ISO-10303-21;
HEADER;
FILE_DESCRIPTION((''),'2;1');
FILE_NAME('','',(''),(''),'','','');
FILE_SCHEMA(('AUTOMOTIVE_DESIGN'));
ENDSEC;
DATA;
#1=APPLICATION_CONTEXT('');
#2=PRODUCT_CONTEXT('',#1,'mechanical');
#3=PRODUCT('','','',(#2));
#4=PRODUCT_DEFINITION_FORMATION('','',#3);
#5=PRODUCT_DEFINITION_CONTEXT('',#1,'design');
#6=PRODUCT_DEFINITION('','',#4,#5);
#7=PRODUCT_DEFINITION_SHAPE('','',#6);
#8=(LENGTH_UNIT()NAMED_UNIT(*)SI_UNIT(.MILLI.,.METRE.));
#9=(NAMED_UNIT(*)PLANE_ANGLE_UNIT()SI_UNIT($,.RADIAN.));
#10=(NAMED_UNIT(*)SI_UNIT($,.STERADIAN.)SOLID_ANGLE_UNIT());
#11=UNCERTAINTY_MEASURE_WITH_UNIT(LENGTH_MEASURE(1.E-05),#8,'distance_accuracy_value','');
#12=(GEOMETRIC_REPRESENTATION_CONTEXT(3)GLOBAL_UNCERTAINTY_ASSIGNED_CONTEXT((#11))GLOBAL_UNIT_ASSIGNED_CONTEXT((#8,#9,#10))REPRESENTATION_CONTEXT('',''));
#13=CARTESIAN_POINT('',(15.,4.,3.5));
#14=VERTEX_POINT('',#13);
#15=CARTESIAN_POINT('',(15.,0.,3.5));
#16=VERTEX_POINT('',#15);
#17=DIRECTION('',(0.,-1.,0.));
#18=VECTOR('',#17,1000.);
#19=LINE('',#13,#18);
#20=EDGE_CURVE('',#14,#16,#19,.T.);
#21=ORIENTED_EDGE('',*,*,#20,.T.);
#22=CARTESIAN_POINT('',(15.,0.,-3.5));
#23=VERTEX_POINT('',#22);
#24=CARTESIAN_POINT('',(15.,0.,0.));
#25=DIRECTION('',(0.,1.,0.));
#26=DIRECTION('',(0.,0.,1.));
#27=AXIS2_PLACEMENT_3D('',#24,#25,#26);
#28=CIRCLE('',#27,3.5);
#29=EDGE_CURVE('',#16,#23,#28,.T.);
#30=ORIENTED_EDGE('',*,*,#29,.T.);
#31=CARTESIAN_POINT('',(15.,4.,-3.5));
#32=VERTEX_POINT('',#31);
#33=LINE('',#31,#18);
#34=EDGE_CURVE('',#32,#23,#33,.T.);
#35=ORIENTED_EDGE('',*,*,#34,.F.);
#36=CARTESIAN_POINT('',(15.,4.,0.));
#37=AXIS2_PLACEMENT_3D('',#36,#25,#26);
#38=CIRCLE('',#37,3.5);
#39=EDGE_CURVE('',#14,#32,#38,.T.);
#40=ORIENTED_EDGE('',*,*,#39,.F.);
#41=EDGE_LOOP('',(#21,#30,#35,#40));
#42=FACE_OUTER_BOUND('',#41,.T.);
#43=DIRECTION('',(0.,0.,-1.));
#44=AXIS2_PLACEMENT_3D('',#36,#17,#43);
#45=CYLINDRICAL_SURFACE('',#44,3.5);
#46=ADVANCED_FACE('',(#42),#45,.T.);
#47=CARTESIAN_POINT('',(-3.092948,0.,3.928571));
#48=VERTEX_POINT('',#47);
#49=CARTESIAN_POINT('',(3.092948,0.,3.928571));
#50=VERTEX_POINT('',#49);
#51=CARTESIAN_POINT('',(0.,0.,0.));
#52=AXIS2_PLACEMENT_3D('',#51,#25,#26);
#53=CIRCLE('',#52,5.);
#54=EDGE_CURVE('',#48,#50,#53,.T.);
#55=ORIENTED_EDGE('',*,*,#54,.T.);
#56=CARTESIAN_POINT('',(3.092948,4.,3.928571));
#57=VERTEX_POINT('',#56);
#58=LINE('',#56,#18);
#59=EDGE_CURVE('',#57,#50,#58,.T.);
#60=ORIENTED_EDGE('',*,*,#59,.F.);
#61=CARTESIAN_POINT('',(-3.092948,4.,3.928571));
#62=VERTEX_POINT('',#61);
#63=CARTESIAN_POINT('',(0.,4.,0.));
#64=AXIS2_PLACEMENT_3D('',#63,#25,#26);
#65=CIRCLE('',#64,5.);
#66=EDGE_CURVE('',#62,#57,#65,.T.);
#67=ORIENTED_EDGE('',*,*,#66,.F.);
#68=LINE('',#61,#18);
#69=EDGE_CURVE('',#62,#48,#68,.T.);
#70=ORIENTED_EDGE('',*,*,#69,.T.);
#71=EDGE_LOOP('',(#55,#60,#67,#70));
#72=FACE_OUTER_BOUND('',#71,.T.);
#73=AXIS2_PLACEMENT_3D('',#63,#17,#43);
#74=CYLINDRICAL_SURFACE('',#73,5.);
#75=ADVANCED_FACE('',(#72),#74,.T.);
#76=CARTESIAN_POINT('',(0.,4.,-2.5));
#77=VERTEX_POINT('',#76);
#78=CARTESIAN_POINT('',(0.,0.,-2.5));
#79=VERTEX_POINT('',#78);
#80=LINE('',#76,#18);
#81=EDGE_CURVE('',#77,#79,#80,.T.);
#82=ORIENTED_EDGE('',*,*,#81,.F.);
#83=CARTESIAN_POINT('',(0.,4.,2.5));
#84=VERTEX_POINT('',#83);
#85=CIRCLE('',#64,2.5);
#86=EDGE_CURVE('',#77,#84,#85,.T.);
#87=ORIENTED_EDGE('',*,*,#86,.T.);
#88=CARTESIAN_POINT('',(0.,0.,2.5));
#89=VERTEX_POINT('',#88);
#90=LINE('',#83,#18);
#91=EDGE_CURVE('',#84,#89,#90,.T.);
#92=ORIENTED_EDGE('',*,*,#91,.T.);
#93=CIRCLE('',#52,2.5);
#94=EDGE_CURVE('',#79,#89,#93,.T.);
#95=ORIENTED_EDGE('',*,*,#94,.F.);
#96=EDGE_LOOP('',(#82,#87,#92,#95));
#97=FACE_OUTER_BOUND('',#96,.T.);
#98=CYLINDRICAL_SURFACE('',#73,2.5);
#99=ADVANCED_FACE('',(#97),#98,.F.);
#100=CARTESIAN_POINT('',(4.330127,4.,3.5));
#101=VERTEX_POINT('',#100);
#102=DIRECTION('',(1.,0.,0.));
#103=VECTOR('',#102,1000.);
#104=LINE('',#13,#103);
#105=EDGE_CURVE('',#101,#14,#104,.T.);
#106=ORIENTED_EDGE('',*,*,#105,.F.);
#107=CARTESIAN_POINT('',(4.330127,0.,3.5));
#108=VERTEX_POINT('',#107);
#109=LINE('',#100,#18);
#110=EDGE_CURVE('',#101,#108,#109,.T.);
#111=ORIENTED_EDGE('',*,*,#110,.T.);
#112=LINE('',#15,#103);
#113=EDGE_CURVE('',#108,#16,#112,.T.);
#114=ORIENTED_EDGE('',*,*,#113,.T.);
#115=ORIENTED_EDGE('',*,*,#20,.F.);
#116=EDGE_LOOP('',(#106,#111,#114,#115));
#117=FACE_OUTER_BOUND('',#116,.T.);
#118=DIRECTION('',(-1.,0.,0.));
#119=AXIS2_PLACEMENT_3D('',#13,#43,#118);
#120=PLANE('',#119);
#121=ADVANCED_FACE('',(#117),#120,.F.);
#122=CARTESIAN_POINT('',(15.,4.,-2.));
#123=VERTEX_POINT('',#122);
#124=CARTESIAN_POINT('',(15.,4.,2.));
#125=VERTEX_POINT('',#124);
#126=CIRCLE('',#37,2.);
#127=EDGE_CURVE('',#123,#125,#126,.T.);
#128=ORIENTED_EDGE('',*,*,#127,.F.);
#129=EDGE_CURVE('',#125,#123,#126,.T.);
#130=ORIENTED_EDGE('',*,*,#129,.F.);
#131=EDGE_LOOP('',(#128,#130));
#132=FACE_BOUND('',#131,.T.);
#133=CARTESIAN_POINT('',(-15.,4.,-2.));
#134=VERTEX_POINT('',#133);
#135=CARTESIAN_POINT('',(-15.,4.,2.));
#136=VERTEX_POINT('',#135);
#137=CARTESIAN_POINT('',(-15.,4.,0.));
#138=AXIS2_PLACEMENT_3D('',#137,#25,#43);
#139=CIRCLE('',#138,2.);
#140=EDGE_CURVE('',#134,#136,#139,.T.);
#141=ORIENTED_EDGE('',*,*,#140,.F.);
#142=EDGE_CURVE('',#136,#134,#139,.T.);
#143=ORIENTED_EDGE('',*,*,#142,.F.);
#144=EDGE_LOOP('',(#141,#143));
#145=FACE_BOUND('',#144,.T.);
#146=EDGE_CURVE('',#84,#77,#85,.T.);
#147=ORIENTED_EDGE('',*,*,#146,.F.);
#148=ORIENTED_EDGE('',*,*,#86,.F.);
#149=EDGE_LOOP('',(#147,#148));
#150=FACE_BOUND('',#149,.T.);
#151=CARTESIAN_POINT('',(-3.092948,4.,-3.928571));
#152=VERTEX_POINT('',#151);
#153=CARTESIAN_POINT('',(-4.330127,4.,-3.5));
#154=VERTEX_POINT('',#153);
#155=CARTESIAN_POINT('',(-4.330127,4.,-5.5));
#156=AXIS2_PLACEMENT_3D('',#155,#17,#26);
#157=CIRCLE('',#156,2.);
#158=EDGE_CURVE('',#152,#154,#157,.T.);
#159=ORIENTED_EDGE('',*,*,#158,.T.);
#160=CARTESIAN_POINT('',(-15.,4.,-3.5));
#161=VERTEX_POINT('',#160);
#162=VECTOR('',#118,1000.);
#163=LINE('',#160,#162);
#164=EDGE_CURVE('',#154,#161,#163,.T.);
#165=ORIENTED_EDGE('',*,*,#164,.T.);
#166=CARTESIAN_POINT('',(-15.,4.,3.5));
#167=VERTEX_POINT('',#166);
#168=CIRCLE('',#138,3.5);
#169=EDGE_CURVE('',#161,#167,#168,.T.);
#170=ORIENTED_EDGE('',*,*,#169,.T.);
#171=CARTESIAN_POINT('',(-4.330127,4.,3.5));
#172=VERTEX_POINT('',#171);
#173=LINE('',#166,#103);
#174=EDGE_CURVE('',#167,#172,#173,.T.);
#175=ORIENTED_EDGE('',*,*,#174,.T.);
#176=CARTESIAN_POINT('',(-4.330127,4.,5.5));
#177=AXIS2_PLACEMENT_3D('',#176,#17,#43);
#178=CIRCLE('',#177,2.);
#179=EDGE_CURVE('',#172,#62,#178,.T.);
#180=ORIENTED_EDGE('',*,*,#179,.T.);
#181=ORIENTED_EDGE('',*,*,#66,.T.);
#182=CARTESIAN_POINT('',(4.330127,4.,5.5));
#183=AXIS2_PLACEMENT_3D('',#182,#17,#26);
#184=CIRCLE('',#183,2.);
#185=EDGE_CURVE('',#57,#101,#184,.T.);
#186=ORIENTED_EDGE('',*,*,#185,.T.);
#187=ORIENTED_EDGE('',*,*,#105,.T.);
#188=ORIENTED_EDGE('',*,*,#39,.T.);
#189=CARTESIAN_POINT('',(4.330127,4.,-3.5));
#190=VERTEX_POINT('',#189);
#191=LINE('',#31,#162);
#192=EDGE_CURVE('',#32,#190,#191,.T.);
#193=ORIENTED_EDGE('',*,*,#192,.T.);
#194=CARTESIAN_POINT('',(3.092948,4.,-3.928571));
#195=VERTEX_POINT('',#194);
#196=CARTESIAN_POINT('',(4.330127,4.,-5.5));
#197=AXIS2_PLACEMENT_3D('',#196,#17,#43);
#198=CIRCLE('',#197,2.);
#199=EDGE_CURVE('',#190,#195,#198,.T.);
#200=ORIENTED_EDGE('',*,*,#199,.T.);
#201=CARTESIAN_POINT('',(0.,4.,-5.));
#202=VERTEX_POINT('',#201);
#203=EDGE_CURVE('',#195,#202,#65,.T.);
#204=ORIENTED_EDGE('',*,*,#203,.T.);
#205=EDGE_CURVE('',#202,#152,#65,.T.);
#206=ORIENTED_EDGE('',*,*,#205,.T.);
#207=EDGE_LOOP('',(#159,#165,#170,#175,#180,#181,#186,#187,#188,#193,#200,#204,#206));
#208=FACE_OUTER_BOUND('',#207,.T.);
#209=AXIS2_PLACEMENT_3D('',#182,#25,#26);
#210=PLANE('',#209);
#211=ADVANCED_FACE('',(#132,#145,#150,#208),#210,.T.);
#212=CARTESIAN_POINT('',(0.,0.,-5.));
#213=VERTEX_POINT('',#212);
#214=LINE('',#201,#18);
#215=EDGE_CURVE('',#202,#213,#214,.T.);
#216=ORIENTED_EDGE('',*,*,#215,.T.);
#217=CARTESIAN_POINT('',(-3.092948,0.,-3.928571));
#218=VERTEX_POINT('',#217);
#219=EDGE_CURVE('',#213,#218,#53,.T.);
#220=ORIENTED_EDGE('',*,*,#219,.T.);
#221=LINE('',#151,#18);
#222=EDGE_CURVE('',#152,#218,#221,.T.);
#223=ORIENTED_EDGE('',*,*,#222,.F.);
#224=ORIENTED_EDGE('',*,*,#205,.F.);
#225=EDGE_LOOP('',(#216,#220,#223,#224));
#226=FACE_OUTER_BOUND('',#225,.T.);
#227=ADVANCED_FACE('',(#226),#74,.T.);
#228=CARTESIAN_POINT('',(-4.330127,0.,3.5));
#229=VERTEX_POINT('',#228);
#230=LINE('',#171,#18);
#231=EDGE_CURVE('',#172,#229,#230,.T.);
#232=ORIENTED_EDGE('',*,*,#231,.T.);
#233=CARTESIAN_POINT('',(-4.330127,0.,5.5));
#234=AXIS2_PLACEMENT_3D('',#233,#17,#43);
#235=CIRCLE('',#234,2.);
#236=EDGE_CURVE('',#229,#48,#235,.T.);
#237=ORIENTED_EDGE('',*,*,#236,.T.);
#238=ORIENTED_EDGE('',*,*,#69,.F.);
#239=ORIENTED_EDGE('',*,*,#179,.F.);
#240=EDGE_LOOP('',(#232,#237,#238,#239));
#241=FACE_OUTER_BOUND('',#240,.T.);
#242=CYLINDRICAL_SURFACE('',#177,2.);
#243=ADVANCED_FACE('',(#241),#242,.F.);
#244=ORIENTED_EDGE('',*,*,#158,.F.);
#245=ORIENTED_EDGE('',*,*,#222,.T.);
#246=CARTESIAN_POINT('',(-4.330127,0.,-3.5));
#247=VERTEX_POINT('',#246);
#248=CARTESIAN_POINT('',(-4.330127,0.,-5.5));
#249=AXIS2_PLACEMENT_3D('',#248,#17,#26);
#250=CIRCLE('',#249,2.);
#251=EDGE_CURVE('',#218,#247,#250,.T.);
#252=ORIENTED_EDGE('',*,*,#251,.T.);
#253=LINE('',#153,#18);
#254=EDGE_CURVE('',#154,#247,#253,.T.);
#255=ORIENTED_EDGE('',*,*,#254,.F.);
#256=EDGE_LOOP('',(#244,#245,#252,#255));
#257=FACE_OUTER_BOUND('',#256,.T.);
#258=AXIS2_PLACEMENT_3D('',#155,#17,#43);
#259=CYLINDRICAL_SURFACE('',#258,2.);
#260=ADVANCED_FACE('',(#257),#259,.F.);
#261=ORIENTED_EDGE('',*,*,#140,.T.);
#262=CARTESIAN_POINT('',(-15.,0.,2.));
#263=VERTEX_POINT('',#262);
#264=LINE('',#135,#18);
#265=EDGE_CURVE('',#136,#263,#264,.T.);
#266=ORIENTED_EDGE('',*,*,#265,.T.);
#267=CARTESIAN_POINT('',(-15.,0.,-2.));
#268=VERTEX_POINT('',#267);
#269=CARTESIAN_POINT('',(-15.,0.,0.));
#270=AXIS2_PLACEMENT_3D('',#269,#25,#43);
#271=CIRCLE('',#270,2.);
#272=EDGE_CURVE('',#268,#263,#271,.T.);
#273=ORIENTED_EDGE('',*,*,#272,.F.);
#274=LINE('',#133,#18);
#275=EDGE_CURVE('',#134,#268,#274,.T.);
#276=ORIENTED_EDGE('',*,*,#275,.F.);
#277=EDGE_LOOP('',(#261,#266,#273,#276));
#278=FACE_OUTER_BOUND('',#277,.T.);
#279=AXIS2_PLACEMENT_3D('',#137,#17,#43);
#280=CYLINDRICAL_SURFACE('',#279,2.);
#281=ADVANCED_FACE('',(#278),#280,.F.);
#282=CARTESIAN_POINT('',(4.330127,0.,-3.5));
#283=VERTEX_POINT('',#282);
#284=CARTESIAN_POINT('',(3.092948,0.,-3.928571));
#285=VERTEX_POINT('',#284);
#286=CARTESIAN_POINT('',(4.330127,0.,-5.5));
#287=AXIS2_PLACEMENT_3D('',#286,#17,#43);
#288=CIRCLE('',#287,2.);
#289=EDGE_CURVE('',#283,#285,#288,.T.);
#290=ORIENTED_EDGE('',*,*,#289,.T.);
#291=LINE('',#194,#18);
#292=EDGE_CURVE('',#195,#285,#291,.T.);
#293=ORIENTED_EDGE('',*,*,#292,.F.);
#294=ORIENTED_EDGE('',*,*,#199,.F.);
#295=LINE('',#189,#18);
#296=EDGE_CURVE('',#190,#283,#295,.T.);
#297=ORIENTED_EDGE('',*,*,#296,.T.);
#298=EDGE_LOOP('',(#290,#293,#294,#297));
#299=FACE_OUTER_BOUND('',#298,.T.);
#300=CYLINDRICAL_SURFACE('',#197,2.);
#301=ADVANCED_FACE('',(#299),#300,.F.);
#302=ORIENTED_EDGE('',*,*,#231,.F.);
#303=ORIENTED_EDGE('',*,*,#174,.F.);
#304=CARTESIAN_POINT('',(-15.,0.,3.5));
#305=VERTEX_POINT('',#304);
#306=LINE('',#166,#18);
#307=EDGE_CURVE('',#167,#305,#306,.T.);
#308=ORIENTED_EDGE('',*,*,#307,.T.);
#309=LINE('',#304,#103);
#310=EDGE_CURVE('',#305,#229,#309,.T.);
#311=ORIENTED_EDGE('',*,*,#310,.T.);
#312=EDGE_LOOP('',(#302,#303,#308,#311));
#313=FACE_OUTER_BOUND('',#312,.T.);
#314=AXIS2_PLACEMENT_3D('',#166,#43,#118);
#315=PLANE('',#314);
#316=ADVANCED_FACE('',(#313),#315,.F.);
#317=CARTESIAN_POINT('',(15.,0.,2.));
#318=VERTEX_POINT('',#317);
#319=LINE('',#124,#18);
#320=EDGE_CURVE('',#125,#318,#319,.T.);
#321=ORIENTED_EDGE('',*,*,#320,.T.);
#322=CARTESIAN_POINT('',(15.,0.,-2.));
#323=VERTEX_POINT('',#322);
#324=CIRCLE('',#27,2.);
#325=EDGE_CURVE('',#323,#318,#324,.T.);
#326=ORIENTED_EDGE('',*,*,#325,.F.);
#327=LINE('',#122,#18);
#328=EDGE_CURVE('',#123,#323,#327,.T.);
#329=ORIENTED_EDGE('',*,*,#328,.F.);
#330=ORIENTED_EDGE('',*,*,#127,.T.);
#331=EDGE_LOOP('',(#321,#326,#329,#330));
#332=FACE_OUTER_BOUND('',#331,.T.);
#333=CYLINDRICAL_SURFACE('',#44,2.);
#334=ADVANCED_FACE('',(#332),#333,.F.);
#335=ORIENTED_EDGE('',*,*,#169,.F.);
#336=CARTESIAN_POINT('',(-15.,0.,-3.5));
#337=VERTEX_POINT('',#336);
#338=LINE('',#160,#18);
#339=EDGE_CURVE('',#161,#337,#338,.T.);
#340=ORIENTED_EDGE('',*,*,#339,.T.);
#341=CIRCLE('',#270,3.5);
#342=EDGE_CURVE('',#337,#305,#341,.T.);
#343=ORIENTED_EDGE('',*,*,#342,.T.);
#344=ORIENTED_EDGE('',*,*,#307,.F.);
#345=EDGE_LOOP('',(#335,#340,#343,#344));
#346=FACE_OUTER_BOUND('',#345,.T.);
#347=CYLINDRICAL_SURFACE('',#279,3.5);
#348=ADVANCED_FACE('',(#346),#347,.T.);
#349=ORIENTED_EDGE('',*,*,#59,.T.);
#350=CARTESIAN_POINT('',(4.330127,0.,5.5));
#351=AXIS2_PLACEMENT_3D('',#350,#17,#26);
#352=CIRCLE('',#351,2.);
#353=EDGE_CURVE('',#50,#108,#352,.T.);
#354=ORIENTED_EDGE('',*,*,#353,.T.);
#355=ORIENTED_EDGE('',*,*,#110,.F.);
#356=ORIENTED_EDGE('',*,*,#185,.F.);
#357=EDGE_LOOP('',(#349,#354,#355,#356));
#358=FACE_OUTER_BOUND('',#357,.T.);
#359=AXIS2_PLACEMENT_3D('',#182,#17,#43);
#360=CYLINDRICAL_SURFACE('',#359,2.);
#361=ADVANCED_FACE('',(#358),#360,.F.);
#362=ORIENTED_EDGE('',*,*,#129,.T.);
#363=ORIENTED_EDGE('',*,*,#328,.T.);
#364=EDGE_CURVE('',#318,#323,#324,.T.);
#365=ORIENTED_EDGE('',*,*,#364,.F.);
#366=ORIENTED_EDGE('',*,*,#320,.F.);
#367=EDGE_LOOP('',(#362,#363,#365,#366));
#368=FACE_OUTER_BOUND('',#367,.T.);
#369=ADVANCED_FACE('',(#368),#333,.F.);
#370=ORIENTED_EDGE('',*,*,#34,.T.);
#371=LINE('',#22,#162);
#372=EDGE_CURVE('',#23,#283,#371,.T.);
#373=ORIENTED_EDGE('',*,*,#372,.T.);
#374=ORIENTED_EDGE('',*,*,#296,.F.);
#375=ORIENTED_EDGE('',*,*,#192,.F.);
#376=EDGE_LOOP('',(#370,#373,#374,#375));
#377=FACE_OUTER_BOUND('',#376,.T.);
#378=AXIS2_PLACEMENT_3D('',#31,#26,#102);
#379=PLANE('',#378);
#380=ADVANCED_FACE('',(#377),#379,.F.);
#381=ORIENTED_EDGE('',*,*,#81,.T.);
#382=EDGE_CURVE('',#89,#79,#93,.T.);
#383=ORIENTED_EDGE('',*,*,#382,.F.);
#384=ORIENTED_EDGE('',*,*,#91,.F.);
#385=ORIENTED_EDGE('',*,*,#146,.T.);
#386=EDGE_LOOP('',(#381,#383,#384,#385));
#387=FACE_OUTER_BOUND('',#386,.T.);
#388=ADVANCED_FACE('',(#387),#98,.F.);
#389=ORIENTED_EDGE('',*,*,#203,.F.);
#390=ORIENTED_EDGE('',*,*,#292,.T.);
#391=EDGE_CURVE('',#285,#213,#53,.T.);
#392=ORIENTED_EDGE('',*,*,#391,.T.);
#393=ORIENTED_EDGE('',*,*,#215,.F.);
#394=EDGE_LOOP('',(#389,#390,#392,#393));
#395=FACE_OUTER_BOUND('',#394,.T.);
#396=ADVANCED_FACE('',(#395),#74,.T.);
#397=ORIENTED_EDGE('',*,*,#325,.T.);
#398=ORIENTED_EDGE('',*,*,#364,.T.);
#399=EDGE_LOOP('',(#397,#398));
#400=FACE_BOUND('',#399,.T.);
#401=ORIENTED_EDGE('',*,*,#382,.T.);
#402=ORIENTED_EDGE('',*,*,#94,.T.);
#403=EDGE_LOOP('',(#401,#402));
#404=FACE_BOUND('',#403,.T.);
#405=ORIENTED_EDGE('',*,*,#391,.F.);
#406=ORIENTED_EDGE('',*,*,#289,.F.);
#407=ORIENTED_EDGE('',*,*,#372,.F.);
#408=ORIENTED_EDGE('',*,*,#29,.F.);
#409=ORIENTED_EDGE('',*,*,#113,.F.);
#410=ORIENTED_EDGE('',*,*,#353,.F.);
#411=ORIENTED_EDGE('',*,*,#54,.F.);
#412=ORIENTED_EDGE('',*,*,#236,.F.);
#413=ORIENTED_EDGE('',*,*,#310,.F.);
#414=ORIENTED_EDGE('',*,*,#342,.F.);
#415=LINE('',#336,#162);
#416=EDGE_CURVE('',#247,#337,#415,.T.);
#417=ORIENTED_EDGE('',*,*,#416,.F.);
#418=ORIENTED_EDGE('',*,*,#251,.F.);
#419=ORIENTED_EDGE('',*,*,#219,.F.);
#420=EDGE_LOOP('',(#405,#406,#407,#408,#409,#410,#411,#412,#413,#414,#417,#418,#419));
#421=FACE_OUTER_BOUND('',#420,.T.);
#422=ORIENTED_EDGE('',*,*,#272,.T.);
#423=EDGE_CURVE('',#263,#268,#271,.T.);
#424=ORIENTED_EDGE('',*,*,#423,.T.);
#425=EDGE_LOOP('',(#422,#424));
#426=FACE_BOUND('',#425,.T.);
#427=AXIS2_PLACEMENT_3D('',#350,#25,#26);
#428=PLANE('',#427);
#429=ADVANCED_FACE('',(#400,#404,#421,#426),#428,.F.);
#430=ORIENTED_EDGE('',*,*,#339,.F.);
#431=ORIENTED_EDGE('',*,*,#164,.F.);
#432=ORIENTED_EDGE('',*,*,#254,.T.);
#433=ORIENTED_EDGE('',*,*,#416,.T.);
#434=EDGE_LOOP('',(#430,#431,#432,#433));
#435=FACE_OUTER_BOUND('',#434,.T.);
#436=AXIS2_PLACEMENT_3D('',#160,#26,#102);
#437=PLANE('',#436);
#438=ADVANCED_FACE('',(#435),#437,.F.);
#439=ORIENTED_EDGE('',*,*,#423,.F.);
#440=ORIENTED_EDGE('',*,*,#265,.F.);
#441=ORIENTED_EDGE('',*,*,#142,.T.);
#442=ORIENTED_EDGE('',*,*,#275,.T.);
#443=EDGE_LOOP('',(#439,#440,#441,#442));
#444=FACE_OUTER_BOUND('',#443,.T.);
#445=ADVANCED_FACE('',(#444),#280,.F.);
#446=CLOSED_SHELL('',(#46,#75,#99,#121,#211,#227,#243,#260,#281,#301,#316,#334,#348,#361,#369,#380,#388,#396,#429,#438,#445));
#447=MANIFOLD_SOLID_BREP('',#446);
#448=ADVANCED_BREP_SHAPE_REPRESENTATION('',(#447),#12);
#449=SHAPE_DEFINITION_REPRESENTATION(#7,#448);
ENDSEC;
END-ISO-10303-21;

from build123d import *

# Parameters (mm, degrees)
SKETCH1_R           = 5
SKETCH1_R_2         = 4
BOSS_EXTRUDE1_DEPTH = 8
SCALE1_SCALE        = 0.5


with BuildPart() as part:
    # Sketch1 → Boss-Extrude1 (new body)
    with BuildSketch(Plane(origin=(0, 0, 0), x_dir=(1, 0, 0), z_dir=(0, 1, 0))):
        with BuildLine():
            Line((30, 7), (8.660254038, 7))
            ThreePointArc((8.660254038, 7), (7.350946696, 7.22035527), (6.185895741, 7.857142857))
            ThreePointArc((6.185895741, 7.857142857), (0, 10), (-6.185895741, 7.857142857))
            ThreePointArc((-6.185895741, 7.857142857), (-7.350946696, 7.22035527), (-8.660254038, 7))
            Line((-8.660254038, 7), (-30, 7))
            ThreePointArc((-30, 7), (-37, 0), (-30, -7))
            Line((-30, -7), (-8.660254038, -7))
            ThreePointArc((-8.660254038, -7), (-7.350946696, -7.22035527), (-6.185895741, -7.857142857))
            ThreePointArc((-6.185895741, -7.857142857), (0, -10), (6.185895741, -7.857142857))
            ThreePointArc((6.185895741, -7.857142857), (7.350946696, -7.22035527), (8.660254038, -7))
            Line((8.660254038, -7), (30, -7))
            ThreePointArc((30, -7), (37, 0), (30, 7))
        make_face()
        with Locations(Location((0, 0, 0), (0, 0, 270))):
            Circle(SKETCH1_R, mode=Mode.SUBTRACT)
        with Locations(Location((30, 0, 0), (0, 0, 270))):
            Circle(SKETCH1_R_2, mode=Mode.SUBTRACT)
        with Locations(Location((-30, 0, 0), (0, 0, 90))):
            Circle(SKETCH1_R_2, mode=Mode.SUBTRACT)
    extrude(amount=BOSS_EXTRUDE1_DEPTH)


with BuildPart() as part_1:
    # Scale1: scaled about (0, 0, 0)
    add(part.part.scale(SCALE1_SCALE))


solid = part_1.part
